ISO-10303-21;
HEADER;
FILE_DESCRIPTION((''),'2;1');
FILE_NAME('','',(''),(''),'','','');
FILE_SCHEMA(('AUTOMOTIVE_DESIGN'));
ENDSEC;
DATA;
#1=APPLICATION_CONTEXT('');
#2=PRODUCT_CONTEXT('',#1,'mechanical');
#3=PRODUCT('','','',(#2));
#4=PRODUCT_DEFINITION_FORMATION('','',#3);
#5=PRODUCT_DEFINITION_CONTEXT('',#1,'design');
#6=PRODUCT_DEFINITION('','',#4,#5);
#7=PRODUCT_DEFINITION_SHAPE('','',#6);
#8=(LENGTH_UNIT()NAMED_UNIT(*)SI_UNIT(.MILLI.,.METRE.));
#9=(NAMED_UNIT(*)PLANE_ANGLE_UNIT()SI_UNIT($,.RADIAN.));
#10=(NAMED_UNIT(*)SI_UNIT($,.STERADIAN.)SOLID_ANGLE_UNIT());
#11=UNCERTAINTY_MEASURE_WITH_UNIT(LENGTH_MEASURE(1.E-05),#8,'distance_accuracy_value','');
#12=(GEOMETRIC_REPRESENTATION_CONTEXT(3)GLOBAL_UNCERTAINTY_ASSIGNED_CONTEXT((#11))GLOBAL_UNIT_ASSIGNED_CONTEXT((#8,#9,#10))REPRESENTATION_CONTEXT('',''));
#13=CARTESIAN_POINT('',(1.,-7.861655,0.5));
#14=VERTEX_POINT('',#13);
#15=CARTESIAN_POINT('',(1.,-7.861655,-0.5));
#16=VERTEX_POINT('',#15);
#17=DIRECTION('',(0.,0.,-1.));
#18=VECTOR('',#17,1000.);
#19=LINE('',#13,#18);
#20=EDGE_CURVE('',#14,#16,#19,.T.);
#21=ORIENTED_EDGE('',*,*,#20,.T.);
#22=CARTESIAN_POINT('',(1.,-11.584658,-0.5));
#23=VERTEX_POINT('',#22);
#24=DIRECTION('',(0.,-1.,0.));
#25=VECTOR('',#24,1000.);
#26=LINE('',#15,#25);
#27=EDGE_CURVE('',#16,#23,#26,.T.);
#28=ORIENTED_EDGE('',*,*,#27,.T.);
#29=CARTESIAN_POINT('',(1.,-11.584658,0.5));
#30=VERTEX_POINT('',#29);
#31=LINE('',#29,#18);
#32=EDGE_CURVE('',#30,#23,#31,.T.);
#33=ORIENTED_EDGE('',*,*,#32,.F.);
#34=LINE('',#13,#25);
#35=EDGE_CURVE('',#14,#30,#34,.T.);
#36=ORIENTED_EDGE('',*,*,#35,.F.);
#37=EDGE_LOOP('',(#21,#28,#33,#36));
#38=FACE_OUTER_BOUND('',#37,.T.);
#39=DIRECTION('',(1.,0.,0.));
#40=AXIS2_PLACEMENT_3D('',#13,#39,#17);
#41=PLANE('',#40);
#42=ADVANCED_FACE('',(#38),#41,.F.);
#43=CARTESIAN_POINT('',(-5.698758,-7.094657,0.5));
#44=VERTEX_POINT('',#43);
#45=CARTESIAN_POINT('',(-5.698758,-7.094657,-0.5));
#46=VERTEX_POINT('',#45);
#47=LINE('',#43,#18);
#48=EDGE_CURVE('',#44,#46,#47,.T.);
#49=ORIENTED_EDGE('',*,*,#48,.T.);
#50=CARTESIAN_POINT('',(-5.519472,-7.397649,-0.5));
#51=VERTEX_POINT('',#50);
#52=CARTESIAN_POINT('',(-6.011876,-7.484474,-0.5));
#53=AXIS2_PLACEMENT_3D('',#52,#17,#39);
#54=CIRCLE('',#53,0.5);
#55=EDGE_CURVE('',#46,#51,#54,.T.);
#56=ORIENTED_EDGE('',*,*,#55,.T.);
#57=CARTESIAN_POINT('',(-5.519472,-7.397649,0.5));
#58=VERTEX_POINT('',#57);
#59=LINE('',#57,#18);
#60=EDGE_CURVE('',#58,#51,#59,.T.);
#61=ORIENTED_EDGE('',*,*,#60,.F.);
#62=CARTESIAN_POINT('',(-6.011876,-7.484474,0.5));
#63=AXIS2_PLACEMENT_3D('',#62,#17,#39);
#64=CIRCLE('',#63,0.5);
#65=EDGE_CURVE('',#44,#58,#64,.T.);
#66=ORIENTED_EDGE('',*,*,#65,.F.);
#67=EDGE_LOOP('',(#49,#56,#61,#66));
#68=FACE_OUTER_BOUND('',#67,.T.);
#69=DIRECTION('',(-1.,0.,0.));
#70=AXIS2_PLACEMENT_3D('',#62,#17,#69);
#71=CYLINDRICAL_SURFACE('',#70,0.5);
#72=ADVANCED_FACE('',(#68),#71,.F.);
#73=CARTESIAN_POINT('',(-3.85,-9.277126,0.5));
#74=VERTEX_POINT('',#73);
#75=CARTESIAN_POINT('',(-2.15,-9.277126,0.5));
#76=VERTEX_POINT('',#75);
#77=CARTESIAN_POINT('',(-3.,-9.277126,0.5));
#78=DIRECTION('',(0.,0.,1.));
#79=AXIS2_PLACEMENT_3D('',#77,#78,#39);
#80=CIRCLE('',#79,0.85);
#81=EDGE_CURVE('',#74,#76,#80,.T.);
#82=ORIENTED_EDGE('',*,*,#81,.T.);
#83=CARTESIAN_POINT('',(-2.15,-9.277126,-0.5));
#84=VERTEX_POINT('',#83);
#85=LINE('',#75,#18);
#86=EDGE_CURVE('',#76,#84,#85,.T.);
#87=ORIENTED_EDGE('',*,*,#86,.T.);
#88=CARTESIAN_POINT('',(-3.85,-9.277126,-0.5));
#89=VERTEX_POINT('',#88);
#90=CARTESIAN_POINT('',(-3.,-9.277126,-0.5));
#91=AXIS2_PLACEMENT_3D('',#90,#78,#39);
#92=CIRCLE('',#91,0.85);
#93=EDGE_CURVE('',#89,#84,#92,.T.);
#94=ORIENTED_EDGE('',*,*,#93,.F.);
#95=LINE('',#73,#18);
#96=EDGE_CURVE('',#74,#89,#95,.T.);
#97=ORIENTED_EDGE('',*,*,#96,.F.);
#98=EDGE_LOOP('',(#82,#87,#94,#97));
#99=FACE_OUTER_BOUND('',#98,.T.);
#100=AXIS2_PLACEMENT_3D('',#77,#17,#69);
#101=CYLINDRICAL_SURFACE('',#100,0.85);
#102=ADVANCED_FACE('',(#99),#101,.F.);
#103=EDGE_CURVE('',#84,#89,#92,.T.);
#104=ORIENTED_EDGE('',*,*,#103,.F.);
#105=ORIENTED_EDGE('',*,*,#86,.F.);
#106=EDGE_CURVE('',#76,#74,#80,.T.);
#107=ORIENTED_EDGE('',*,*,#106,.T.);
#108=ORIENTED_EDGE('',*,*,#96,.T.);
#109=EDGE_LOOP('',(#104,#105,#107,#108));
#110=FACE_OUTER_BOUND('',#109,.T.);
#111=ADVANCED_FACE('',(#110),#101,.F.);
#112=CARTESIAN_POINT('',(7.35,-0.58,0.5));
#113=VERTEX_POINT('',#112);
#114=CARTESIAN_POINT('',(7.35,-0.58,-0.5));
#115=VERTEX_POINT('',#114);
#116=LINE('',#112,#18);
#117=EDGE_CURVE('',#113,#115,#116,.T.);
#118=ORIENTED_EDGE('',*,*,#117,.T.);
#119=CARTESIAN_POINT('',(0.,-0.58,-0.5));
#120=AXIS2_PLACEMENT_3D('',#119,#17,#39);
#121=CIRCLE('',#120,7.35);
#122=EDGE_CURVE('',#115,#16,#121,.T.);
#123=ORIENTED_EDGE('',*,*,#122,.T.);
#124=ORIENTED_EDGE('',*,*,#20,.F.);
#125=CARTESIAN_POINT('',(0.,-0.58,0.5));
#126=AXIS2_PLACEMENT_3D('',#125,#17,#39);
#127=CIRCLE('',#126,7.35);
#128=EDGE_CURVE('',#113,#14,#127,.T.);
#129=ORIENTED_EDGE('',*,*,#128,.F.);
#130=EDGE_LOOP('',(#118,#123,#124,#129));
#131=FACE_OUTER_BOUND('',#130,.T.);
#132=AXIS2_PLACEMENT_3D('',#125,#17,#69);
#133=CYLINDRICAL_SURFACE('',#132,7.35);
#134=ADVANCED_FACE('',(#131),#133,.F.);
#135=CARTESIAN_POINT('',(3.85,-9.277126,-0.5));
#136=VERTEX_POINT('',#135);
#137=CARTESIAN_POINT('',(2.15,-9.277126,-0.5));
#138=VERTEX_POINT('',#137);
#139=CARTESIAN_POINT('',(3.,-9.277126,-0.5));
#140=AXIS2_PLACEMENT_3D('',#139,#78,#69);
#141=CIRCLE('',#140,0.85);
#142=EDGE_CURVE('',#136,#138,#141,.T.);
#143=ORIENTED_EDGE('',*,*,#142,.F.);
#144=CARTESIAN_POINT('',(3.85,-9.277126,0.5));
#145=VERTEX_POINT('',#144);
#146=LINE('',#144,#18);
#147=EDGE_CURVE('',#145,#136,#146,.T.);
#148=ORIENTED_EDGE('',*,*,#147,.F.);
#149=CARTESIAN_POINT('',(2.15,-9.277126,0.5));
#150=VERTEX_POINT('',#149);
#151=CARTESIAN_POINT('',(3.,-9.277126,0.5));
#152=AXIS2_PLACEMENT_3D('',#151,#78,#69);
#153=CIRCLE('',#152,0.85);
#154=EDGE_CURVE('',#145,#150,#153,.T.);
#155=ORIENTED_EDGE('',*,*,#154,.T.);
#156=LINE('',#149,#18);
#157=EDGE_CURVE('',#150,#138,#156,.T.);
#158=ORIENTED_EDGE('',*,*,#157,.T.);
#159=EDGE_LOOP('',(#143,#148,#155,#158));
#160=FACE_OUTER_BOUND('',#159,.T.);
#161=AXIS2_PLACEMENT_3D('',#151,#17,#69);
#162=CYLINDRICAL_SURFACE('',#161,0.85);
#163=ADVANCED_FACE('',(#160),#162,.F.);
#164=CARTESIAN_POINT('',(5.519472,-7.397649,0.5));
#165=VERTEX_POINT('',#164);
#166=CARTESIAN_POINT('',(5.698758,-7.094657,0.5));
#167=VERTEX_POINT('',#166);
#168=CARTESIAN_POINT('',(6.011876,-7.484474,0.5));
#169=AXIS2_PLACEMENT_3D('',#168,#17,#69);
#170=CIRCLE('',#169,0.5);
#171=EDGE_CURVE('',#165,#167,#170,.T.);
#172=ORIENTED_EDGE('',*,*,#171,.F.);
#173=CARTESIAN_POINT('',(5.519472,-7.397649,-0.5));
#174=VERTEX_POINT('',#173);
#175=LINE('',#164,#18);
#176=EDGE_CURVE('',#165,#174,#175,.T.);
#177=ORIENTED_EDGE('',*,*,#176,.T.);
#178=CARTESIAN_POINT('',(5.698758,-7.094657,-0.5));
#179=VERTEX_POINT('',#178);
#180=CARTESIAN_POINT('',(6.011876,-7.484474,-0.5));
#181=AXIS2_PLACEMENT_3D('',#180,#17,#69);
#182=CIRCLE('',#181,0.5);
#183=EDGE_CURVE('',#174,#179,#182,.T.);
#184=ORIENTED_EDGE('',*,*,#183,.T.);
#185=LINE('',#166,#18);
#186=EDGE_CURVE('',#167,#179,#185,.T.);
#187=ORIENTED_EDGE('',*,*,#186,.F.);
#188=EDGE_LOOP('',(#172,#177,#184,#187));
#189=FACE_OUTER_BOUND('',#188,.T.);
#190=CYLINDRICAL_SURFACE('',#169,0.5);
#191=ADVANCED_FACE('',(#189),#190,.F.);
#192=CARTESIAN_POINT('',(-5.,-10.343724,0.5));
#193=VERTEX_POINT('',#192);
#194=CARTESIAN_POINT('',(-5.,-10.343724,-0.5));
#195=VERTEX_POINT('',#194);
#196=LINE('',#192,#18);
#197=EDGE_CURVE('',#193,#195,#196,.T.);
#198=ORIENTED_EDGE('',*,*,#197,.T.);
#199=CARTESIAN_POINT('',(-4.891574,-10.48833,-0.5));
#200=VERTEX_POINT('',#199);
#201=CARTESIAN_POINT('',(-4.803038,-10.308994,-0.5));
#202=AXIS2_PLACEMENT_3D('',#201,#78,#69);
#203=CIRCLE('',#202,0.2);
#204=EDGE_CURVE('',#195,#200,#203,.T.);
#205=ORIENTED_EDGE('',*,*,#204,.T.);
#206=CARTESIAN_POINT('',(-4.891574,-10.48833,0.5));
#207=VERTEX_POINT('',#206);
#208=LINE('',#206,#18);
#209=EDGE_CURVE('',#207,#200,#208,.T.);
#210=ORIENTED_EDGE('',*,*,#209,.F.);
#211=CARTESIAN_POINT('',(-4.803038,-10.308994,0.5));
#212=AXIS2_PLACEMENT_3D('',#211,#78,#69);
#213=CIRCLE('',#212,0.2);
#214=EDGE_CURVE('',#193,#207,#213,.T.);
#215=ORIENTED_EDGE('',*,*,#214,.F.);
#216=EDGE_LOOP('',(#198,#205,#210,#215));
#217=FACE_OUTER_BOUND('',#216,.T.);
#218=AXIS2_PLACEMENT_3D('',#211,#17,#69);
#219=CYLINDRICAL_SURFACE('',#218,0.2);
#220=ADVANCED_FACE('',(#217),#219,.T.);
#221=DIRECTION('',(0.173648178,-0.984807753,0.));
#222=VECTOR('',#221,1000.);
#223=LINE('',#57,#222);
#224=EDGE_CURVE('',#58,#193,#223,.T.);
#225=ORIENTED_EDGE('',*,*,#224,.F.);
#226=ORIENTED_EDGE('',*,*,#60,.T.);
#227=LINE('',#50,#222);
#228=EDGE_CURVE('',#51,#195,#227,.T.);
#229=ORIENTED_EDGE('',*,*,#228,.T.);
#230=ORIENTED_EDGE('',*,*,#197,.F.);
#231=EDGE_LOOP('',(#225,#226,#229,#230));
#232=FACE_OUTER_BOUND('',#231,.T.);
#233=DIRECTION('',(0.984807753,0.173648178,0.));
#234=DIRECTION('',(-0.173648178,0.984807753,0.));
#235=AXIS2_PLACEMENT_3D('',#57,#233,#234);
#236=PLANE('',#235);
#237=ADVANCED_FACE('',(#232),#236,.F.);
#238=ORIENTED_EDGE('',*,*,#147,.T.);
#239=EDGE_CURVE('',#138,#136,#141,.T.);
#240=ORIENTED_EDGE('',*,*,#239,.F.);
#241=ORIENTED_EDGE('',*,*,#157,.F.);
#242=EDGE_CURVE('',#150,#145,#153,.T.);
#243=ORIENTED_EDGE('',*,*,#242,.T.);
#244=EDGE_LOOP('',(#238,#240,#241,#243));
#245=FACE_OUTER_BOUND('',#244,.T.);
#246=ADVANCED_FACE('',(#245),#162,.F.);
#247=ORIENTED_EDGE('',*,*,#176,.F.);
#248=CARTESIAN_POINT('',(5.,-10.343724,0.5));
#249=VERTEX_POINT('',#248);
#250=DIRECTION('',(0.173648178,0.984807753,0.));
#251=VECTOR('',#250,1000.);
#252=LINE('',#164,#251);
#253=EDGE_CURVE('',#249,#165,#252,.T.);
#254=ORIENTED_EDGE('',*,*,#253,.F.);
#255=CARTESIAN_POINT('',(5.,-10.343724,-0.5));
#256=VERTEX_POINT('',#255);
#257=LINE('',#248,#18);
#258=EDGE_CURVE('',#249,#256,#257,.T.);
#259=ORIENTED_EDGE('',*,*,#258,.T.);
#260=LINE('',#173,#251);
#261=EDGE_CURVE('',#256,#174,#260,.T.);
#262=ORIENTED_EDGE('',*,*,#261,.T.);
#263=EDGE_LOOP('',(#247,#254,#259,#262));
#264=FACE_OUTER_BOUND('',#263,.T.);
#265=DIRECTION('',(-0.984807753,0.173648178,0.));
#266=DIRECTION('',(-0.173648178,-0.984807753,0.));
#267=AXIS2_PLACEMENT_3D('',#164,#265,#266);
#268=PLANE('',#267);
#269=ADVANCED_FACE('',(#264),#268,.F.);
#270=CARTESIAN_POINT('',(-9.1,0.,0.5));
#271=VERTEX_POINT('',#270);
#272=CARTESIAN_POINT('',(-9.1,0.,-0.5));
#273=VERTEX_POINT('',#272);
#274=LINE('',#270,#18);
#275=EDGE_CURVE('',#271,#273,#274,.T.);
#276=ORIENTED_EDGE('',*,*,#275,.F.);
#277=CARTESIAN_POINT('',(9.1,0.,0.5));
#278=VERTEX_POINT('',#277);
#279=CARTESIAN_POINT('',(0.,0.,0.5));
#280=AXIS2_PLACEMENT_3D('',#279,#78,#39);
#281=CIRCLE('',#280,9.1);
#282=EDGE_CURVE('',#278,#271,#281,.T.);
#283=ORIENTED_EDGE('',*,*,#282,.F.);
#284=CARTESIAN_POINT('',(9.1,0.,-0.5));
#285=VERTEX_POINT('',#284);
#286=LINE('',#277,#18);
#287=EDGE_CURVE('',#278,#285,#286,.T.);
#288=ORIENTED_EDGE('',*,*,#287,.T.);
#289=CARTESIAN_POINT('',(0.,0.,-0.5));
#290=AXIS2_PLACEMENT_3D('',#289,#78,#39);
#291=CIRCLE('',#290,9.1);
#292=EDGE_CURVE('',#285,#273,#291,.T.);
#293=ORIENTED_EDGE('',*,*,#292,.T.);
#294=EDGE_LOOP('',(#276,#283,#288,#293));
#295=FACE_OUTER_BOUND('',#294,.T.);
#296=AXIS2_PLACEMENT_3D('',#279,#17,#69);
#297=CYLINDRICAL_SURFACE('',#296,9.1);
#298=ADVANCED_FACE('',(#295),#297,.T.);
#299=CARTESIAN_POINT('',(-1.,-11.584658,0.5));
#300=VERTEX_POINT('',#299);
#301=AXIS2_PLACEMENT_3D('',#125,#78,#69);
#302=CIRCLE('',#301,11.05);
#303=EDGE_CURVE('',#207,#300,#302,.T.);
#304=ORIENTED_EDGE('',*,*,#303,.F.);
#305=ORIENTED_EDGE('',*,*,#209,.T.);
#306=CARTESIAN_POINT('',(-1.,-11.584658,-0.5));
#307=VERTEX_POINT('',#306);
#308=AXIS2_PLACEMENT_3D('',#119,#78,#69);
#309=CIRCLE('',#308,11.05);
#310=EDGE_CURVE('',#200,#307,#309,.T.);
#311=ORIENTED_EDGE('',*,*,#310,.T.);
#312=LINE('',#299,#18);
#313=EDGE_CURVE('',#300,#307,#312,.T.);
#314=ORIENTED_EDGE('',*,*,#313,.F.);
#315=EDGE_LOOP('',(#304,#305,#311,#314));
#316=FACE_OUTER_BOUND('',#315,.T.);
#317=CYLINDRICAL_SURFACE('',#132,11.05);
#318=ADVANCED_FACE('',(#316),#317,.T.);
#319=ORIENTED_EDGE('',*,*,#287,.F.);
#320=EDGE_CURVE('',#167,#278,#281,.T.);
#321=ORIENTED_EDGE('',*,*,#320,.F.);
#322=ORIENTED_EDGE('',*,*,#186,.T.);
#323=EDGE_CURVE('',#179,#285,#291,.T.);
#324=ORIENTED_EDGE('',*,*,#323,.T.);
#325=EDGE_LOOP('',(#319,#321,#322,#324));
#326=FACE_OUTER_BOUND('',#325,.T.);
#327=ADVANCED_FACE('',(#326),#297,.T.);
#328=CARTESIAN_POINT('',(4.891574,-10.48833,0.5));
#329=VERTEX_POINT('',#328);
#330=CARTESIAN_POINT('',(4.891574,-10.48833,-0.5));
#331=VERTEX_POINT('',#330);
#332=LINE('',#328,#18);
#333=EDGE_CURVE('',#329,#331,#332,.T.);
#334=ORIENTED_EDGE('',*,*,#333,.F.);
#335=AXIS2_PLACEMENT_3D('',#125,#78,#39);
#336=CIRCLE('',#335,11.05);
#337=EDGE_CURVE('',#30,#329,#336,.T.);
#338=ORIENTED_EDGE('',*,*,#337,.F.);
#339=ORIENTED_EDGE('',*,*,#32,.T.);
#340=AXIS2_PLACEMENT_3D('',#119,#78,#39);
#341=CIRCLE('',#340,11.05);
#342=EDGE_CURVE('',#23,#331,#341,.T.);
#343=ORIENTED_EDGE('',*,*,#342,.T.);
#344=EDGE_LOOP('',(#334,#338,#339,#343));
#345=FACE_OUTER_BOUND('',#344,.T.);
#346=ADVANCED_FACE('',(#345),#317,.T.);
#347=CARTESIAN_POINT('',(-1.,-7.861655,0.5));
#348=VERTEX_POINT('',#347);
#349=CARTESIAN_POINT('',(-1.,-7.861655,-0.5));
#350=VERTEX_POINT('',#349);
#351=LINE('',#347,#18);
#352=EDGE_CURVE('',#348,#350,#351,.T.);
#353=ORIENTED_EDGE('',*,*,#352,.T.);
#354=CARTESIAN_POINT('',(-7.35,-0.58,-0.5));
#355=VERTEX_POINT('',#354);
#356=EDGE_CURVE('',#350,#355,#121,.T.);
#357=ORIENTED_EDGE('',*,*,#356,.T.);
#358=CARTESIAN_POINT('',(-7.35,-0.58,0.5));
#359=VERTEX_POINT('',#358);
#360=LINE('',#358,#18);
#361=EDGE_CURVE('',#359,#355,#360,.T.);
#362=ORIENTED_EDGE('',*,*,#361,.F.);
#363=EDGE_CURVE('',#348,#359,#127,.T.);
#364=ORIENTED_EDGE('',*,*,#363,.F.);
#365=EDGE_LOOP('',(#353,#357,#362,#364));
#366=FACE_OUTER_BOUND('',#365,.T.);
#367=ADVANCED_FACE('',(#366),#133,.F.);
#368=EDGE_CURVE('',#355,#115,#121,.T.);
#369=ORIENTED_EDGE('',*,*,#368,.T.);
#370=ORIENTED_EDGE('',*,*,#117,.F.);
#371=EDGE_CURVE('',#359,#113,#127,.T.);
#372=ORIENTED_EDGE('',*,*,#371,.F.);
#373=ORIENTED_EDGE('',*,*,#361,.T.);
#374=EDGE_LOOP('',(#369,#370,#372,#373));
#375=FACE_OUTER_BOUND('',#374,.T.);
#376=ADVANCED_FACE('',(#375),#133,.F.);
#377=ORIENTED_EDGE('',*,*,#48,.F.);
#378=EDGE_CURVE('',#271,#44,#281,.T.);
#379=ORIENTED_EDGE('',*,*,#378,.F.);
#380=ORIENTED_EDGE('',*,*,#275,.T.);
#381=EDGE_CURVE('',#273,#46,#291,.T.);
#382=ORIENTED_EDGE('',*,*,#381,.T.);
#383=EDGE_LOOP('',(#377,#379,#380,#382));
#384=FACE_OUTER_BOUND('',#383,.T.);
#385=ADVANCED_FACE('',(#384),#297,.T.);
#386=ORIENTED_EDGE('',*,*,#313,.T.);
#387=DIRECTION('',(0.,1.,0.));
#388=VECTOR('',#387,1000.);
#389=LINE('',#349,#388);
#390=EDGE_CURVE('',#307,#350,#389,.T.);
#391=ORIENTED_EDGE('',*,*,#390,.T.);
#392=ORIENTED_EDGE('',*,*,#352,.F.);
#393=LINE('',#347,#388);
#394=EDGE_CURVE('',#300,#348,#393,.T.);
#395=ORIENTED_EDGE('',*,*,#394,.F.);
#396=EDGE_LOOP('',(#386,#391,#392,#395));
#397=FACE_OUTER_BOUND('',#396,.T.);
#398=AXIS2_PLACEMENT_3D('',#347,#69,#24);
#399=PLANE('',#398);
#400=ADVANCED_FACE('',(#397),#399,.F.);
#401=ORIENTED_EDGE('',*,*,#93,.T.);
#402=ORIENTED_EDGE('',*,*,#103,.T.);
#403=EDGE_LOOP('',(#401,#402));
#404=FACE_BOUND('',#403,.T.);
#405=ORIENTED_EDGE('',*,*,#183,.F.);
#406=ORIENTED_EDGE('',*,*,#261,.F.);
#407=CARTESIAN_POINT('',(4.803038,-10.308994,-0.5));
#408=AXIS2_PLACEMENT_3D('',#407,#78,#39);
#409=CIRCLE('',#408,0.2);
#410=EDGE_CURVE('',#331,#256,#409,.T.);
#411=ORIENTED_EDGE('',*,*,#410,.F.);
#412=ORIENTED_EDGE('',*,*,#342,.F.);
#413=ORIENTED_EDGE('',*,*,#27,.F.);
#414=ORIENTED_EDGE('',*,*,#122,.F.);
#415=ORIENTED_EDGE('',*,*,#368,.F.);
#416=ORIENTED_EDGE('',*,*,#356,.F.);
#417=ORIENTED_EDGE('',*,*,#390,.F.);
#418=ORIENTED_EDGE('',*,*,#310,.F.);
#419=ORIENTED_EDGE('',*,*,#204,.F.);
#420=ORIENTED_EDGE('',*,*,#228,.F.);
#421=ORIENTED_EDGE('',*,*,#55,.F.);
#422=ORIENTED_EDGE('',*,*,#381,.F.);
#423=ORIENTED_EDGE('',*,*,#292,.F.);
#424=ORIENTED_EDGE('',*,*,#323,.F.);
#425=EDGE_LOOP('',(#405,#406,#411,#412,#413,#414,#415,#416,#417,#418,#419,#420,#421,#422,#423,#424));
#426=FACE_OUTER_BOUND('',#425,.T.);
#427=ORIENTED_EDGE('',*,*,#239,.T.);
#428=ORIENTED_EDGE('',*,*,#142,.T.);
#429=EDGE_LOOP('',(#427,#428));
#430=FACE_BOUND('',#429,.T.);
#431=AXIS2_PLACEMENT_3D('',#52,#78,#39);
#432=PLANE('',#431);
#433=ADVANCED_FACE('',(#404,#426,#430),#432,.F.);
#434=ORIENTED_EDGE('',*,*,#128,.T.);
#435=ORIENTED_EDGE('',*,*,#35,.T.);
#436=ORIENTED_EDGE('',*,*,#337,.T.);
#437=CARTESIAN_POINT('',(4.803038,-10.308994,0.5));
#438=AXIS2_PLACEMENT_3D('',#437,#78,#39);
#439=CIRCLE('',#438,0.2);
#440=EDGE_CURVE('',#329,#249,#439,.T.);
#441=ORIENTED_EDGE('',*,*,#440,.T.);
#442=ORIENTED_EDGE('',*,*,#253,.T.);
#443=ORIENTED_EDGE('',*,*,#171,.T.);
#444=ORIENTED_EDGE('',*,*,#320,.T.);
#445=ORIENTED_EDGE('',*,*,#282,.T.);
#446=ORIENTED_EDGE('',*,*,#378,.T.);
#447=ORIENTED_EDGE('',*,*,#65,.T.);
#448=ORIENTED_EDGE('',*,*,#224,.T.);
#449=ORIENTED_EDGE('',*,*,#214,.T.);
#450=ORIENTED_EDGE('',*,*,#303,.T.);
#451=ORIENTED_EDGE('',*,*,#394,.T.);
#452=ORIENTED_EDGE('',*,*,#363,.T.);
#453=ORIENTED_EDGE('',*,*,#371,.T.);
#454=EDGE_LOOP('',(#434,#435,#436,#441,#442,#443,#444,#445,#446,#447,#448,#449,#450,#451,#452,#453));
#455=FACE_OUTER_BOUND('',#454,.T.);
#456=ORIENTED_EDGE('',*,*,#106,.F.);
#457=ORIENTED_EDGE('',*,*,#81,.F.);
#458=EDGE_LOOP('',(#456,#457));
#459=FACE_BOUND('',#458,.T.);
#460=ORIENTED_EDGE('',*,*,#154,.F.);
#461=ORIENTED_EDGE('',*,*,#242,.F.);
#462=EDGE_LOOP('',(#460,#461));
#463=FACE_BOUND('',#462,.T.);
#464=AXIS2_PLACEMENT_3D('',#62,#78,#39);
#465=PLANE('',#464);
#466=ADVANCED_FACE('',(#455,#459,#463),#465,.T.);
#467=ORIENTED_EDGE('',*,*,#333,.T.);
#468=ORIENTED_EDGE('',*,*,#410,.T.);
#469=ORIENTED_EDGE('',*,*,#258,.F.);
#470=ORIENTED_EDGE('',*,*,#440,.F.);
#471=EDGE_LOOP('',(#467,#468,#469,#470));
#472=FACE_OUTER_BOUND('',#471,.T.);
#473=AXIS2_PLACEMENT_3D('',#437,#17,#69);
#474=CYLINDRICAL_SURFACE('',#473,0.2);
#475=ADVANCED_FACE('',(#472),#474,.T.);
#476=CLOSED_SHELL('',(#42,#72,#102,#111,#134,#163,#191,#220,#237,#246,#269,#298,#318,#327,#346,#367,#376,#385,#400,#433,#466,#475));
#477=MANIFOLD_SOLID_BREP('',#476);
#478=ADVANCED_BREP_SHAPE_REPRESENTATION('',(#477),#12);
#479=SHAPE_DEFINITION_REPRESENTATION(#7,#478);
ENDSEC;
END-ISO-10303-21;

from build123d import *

# Parameters (mm, degrees)
BASE_EXTRUDE_DEPTH      = 0.5
BASE_EXTRUDE_DEPTH_BACK = 0.5
SKETCH1_R               = 0.85


with BuildPart() as part:
    # Sketch1 → Base-Extrude (new, two sides: drawn at the far end of the back side and taken through both)
    with BuildSketch(Plane.XY.offset(-BASE_EXTRUDE_DEPTH_BACK)):
        with BuildLine():
            Line((-1, -7.861655032), (-1, -11.584658105))
            ThreePointArc((-1, -11.584658105), (-2.996355114, -11.21599342), (-4.89157372, -10.488330159))
            ThreePointArc((-4.89157372, -10.488330159), (-4.963053699, -10.428973531), (-5, -10.343723502))
            Line((-5, -10.343723502), (-5.51947234, -7.397649464))
            ThreePointArc((-5.51947234, -7.397649464), (-5.581565084, -7.229851618), (-5.698757664, -7.094657221))
            ThreePointArc((-5.698757664, -7.094657221), (0, 9.1), (5.698757664, -7.094657221))
            ThreePointArc((5.698757664, -7.094657221), (5.581565084, -7.229851618), (5.51947234, -7.397649464))
            Line((5.51947234, -7.397649464), (5, -10.343723502))
            ThreePointArc((5, -10.343723502), (4.963053699, -10.428973531), (4.89157372, -10.488330159))
            ThreePointArc((4.89157372, -10.488330159), (2.996355114, -11.21599342), (1, -11.584658105))
            Line((1, -11.584658105), (1, -7.861655032))
            ThreePointArc((1, -7.861655032), (0, 6.77), (-1, -7.861655032))
        make_face()
        with Locations((-3, -9.277125962)):
            Circle(SKETCH1_R, mode=Mode.SUBTRACT)
        with Locations(Location((3, -9.277125962, 0), (0, 0, 180))):
            Circle(SKETCH1_R, mode=Mode.SUBTRACT)
    extrude(amount=BASE_EXTRUDE_DEPTH + BASE_EXTRUDE_DEPTH_BACK)


solid = part.part
